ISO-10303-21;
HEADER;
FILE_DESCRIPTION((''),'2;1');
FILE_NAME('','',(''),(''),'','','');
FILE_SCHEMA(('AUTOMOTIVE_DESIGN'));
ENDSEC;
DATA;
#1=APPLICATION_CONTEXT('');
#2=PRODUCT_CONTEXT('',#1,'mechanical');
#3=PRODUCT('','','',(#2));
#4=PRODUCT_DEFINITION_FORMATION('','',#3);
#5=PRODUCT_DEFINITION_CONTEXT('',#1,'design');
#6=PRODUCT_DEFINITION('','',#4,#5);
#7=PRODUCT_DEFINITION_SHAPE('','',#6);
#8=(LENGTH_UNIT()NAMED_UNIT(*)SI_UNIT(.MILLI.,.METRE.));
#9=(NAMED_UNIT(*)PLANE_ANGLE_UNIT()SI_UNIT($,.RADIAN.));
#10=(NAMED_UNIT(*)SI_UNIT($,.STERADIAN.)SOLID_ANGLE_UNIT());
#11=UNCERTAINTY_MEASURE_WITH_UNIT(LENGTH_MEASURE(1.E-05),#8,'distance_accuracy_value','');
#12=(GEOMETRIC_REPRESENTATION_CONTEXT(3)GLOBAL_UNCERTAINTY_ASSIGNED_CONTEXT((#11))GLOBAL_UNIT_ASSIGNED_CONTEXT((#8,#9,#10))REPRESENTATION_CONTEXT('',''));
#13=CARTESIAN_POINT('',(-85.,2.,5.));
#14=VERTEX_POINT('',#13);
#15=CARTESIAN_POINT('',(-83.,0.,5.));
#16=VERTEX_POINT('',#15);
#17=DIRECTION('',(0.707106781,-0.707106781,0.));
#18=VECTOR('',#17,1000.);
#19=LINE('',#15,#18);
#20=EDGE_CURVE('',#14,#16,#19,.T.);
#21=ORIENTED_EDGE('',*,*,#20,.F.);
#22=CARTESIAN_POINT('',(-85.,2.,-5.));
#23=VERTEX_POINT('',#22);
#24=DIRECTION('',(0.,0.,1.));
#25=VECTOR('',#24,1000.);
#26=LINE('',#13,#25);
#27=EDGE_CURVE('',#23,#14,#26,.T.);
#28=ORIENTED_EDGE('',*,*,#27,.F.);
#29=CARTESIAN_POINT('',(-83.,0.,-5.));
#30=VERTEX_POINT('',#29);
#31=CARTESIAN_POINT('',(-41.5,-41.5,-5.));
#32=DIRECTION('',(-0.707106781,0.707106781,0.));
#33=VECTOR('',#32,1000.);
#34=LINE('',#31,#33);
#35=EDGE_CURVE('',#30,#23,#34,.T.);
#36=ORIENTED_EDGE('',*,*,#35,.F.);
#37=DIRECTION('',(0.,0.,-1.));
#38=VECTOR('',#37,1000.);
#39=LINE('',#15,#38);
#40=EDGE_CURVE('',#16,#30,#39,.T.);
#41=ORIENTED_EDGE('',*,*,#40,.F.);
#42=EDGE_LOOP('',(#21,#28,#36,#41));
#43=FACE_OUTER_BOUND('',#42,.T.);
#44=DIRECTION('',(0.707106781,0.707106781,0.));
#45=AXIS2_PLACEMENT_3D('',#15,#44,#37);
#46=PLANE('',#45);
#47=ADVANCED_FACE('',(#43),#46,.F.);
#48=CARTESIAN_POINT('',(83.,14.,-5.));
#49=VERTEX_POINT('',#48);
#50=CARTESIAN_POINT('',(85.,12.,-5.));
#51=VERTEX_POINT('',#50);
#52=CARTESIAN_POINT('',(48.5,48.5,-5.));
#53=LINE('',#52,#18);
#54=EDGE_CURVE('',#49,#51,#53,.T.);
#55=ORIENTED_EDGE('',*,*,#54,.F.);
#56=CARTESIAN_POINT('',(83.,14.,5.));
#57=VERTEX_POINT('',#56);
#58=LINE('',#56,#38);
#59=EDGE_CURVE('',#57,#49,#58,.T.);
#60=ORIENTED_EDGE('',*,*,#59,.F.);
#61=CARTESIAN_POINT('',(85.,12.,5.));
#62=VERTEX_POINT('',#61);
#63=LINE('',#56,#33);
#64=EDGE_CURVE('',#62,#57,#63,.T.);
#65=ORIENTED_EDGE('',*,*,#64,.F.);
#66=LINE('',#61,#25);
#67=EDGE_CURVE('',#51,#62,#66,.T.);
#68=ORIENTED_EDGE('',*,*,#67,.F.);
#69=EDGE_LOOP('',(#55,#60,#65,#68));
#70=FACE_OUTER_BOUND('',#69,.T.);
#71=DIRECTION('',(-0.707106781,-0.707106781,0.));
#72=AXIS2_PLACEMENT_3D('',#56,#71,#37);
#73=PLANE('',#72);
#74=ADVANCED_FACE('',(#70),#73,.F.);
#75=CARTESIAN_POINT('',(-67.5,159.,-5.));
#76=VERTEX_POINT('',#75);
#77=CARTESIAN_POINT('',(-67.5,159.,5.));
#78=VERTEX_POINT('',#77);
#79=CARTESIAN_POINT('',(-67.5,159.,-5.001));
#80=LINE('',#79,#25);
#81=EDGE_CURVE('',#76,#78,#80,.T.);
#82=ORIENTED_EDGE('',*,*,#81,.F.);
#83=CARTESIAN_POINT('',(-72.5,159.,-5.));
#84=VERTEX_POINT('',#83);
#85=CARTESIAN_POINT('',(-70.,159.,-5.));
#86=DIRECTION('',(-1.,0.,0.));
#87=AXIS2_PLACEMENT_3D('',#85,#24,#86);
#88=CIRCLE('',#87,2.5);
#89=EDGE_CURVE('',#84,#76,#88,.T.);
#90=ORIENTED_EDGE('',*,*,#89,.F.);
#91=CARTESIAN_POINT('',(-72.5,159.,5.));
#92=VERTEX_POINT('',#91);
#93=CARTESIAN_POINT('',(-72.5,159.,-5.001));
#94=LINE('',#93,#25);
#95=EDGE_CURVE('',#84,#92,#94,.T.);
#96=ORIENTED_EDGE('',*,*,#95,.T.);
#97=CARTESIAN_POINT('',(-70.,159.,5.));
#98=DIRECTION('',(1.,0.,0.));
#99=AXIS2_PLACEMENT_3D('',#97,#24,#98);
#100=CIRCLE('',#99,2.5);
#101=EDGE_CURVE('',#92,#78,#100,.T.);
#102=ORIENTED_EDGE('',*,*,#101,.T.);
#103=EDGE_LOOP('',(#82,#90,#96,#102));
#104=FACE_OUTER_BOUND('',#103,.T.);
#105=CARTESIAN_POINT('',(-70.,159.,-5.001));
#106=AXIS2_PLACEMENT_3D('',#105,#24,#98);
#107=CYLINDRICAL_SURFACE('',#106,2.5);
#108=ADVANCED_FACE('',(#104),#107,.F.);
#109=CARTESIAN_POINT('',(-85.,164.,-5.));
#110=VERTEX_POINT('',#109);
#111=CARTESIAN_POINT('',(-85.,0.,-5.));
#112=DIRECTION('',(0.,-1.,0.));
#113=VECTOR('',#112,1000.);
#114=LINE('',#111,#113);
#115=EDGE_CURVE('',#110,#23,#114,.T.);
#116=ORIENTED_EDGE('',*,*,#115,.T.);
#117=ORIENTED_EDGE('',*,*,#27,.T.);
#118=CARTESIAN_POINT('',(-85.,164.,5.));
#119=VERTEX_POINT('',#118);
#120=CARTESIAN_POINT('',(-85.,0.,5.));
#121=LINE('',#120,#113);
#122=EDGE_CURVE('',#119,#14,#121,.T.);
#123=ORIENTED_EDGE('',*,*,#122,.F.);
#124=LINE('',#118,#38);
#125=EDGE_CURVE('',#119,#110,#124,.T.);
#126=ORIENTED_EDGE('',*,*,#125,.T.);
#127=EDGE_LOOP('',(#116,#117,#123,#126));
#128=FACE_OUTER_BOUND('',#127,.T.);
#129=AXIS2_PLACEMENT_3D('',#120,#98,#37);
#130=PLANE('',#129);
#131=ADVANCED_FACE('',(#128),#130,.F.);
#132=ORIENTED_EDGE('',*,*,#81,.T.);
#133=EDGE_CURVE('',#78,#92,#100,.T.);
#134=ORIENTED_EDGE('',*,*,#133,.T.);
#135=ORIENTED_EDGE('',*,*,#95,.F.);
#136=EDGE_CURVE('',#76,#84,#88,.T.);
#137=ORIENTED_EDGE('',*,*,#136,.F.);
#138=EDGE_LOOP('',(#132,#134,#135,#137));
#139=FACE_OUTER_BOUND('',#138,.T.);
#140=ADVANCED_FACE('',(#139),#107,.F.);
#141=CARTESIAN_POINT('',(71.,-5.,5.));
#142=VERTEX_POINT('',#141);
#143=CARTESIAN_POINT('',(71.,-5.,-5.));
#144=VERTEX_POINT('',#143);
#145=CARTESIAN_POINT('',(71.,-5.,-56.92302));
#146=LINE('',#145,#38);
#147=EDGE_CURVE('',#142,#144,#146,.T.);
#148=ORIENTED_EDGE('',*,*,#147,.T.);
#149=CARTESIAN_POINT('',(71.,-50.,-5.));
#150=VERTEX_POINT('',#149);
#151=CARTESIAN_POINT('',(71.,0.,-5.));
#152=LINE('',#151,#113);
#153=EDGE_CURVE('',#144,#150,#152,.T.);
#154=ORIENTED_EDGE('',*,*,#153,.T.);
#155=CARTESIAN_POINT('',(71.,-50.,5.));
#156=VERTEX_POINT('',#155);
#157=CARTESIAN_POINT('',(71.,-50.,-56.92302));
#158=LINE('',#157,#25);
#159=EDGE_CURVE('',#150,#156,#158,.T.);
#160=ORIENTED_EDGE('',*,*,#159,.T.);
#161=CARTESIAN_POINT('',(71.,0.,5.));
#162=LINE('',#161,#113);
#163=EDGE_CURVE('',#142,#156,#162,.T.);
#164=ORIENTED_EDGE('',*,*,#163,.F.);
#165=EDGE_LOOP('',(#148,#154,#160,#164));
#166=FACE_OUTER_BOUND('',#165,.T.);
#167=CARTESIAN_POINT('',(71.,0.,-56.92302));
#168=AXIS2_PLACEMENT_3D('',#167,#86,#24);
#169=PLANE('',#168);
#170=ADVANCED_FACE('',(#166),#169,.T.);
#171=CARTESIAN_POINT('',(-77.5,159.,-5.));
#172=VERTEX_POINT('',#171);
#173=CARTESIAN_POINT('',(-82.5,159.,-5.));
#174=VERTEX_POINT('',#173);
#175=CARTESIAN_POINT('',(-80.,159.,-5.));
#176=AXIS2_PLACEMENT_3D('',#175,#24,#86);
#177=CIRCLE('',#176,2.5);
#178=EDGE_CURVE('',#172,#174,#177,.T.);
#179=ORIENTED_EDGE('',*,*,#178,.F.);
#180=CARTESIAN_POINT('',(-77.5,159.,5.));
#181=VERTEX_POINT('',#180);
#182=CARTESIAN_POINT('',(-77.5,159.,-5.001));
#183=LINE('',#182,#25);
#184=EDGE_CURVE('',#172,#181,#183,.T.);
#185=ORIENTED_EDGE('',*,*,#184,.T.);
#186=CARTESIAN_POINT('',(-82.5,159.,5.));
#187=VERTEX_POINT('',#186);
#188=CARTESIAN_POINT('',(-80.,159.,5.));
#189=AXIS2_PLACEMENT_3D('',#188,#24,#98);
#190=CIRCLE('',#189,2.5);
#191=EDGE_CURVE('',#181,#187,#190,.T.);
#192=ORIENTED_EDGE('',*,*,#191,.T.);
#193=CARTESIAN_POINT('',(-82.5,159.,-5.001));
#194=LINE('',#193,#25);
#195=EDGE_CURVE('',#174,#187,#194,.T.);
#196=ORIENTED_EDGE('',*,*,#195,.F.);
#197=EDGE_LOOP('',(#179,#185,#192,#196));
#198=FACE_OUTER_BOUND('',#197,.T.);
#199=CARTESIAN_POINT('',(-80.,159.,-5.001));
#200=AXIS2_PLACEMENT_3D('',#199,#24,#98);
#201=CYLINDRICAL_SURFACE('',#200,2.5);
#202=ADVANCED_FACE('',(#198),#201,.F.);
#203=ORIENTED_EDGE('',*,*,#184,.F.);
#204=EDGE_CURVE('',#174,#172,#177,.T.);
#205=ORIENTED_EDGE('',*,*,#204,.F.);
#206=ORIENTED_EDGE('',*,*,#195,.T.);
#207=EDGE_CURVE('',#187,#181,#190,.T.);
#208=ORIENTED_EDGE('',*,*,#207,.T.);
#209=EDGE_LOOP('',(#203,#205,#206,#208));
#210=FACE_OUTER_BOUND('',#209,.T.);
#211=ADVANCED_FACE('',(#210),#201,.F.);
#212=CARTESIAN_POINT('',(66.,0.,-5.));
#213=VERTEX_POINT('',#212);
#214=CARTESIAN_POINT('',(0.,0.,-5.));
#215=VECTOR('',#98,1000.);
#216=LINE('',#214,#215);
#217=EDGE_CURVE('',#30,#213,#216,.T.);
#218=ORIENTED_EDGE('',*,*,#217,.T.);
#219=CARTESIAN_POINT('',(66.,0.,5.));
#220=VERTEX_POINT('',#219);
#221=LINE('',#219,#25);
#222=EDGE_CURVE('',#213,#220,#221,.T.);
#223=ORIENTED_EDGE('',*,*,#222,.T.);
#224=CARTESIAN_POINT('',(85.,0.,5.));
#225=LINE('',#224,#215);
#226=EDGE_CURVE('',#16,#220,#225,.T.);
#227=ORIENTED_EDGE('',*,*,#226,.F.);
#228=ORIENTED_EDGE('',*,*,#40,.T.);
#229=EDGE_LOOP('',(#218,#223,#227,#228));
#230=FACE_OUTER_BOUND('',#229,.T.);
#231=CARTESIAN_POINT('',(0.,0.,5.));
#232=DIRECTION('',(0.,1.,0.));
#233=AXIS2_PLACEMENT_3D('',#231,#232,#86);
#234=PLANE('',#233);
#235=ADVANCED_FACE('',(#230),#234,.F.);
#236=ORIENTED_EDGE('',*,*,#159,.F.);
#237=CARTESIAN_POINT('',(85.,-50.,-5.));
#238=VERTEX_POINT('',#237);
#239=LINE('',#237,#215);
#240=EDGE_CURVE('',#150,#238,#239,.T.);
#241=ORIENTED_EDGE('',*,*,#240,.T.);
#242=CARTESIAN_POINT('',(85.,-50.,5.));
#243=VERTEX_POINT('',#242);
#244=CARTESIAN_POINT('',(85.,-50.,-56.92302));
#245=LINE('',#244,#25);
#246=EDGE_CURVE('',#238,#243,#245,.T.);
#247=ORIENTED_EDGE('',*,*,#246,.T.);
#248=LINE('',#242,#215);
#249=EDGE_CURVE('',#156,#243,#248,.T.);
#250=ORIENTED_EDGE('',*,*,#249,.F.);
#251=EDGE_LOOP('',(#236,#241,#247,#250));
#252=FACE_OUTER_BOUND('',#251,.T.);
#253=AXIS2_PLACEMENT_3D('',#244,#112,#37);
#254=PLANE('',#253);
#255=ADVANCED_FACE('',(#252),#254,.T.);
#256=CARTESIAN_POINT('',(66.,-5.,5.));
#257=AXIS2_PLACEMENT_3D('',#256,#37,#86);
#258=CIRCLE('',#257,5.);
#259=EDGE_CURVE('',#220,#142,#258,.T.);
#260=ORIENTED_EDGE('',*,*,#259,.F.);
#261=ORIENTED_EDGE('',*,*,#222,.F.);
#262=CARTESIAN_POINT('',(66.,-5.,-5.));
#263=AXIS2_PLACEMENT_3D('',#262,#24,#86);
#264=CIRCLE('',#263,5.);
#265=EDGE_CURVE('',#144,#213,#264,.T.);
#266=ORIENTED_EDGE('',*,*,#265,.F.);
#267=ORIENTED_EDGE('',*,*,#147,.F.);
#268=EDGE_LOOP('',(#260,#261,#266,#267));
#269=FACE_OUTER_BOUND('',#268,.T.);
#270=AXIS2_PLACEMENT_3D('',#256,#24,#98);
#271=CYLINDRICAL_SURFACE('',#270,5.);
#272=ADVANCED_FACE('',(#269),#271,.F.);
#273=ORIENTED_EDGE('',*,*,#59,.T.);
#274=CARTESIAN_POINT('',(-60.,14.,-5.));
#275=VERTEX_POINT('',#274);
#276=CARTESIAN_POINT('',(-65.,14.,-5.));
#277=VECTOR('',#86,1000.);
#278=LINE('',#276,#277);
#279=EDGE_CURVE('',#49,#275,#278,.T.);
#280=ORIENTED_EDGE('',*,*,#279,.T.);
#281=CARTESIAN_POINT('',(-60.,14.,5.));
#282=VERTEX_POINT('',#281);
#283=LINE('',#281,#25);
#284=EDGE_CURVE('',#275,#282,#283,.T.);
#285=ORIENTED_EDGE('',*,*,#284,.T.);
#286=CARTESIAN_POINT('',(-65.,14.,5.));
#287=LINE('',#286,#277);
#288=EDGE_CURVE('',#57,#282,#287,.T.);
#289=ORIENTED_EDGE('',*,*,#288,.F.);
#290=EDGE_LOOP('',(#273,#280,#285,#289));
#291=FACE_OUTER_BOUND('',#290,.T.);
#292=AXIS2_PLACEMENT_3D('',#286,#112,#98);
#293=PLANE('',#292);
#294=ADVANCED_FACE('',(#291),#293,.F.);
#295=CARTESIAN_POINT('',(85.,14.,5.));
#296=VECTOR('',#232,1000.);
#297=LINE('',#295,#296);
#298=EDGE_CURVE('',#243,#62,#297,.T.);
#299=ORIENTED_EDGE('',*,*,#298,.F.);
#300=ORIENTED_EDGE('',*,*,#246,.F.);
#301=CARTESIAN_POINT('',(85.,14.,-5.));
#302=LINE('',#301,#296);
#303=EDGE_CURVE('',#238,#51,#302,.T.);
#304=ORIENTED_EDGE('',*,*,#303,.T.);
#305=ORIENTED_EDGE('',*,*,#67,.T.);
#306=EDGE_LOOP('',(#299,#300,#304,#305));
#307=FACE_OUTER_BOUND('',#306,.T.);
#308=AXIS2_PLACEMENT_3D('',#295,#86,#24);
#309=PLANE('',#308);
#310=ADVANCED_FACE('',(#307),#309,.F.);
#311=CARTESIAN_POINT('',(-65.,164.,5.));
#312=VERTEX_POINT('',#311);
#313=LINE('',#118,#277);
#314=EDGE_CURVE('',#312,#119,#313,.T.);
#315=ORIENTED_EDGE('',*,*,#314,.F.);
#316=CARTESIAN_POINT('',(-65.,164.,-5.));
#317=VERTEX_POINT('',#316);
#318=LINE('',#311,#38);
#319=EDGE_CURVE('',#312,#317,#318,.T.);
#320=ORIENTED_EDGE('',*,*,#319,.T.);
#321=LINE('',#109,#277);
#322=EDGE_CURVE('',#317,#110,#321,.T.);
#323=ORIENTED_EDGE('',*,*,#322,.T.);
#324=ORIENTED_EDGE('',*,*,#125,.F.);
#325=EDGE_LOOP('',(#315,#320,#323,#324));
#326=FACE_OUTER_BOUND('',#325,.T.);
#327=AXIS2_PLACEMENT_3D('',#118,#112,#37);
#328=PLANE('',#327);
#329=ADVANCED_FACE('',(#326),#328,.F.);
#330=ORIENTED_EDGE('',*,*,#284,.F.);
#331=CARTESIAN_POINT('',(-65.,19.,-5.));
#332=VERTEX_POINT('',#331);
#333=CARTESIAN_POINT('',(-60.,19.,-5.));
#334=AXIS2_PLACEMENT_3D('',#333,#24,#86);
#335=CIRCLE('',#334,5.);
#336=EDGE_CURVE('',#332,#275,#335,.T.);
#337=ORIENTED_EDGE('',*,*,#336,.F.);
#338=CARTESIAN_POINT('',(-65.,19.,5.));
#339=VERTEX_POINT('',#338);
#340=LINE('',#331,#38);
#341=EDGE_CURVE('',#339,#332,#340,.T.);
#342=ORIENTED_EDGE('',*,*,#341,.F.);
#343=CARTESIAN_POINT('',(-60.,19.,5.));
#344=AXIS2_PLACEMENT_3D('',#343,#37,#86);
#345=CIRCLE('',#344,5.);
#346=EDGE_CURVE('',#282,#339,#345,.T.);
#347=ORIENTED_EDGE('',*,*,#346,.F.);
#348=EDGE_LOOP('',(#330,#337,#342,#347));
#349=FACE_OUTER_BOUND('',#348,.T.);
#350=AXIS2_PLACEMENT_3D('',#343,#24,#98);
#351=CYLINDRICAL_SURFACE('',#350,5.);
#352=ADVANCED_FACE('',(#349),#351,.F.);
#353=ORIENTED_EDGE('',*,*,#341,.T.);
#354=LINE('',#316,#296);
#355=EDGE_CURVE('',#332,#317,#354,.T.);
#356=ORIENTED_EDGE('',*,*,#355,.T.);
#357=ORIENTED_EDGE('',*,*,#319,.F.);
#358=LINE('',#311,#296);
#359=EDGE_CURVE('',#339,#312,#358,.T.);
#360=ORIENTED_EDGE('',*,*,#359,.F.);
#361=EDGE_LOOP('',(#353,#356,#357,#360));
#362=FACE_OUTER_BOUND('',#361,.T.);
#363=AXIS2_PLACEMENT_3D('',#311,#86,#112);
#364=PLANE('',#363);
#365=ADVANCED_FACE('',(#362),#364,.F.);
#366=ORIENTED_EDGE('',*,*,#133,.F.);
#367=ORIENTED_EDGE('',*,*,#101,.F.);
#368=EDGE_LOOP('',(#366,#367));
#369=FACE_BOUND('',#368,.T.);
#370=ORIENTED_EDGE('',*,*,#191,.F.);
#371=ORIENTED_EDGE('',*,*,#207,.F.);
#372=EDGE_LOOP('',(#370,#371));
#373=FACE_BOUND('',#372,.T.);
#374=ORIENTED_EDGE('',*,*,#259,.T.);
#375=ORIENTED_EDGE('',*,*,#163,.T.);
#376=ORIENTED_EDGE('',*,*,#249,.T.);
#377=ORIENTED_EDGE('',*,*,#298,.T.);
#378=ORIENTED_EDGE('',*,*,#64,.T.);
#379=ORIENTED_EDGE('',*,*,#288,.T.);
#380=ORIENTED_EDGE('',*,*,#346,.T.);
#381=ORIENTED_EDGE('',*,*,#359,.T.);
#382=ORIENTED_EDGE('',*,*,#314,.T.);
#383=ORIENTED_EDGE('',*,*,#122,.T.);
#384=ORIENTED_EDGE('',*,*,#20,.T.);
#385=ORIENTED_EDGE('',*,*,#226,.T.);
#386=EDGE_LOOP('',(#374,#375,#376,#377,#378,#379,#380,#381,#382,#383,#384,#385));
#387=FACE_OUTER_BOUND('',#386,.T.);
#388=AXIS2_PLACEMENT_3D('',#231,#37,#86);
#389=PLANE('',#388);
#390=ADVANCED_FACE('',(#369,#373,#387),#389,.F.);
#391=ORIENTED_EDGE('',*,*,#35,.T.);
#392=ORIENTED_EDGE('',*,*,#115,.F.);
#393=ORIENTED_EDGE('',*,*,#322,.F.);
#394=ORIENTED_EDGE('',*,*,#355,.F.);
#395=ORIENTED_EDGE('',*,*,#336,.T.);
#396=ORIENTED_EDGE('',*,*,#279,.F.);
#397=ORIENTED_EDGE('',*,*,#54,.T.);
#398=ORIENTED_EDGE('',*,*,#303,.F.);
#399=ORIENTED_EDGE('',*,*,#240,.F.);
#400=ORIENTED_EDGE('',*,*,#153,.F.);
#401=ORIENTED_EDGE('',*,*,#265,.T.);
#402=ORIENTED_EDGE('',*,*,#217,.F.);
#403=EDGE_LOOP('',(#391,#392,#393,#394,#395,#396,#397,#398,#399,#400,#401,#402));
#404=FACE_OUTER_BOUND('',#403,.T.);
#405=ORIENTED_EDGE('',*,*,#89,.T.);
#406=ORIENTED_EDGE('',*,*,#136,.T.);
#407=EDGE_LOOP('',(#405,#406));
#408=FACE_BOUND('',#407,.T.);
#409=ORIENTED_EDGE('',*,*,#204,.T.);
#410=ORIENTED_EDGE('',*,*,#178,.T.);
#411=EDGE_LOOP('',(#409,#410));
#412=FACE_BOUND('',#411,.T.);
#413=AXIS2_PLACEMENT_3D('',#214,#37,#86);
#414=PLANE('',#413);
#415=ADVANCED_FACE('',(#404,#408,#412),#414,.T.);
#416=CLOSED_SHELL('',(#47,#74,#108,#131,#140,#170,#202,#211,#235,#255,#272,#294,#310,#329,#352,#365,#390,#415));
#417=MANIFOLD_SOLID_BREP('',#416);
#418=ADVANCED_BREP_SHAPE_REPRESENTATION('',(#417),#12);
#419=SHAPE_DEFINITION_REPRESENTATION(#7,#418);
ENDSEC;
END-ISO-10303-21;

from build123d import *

# Parameters (mm, degrees)
EXTRUDE_1_DEPTH     = 5
CUT_EXTRUDE_1_REACH = 186.989
SKETCH_2_R          = 2.5
SKETCH_3_W          = 14
SKETCH_3_H          = 50
EXTRUDE_2_DEPTH     = 10
FILLET_1_R          = 5
CHAMFER_1_SIZE      = 2


with BuildPart() as part:
    # 草图1 → 凸台-拉伸1 (new, symmetric)
    with BuildSketch(Plane.XY):
        Polygon((0, 0), (-85, 0), (-85, 164), (-65, 164), (-65, 14), (85, 14), (85, 0), align=None)
    extrude(amount=EXTRUDE_1_DEPTH, both=True)

    # 草图2 → 切除-拉伸1 (cut, up to next)
    with BuildSketch(Plane.XY.offset(5), mode=Mode.PRIVATE) as cut_extrude_1_sk1:
        with Locations((-80, 159)):
            Circle(SKETCH_2_R)
    cut_extrude_1_tool1 = extrude(cut_extrude_1_sk1.sketch, amount=-CUT_EXTRUDE_1_REACH, mode=Mode.PRIVATE) & part.part
    # 草图2 → 切除-拉伸1 (cut, up to next)
    with BuildSketch(Plane.XY.offset(5), mode=Mode.PRIVATE) as cut_extrude_1_sk2:
        with Locations((-70, 159)):
            Circle(SKETCH_2_R)
    cut_extrude_1_tool2 = extrude(cut_extrude_1_sk2.sketch, amount=-CUT_EXTRUDE_1_REACH, mode=Mode.PRIVATE) & part.part
    add(cut_extrude_1_tool1.solids().sort_by_distance((-80, 159, 5))[0], mode=Mode.SUBTRACT)
    add(cut_extrude_1_tool2.solids().sort_by_distance((-70, 159, 5))[0], mode=Mode.SUBTRACT)

    # 草图3 → 凸台-拉伸2 (add)
    with BuildSketch(Plane.XY.offset(5)):
        with Locations((78, -25)):
            Rectangle(SKETCH_3_W, SKETCH_3_H)
    extrude(amount=-EXTRUDE_2_DEPTH)

    # 圆角1
    fillet_1_edges = [part.edges().sort_by_distance(p)[0] for p in [
        (-65, 14, 0),
        (71, 0, 0),
    ]]
    fillet(fillet_1_edges, radius=FILLET_1_R)

    # 倒角1
    chamfer_1_edges = [part.edges().sort_by_distance(p)[0] for p in [
        (-85, 0, 0),
        (85, 14, 0),
    ]]
    chamfer(chamfer_1_edges, length=CHAMFER_1_SIZE)


solid = part.part
